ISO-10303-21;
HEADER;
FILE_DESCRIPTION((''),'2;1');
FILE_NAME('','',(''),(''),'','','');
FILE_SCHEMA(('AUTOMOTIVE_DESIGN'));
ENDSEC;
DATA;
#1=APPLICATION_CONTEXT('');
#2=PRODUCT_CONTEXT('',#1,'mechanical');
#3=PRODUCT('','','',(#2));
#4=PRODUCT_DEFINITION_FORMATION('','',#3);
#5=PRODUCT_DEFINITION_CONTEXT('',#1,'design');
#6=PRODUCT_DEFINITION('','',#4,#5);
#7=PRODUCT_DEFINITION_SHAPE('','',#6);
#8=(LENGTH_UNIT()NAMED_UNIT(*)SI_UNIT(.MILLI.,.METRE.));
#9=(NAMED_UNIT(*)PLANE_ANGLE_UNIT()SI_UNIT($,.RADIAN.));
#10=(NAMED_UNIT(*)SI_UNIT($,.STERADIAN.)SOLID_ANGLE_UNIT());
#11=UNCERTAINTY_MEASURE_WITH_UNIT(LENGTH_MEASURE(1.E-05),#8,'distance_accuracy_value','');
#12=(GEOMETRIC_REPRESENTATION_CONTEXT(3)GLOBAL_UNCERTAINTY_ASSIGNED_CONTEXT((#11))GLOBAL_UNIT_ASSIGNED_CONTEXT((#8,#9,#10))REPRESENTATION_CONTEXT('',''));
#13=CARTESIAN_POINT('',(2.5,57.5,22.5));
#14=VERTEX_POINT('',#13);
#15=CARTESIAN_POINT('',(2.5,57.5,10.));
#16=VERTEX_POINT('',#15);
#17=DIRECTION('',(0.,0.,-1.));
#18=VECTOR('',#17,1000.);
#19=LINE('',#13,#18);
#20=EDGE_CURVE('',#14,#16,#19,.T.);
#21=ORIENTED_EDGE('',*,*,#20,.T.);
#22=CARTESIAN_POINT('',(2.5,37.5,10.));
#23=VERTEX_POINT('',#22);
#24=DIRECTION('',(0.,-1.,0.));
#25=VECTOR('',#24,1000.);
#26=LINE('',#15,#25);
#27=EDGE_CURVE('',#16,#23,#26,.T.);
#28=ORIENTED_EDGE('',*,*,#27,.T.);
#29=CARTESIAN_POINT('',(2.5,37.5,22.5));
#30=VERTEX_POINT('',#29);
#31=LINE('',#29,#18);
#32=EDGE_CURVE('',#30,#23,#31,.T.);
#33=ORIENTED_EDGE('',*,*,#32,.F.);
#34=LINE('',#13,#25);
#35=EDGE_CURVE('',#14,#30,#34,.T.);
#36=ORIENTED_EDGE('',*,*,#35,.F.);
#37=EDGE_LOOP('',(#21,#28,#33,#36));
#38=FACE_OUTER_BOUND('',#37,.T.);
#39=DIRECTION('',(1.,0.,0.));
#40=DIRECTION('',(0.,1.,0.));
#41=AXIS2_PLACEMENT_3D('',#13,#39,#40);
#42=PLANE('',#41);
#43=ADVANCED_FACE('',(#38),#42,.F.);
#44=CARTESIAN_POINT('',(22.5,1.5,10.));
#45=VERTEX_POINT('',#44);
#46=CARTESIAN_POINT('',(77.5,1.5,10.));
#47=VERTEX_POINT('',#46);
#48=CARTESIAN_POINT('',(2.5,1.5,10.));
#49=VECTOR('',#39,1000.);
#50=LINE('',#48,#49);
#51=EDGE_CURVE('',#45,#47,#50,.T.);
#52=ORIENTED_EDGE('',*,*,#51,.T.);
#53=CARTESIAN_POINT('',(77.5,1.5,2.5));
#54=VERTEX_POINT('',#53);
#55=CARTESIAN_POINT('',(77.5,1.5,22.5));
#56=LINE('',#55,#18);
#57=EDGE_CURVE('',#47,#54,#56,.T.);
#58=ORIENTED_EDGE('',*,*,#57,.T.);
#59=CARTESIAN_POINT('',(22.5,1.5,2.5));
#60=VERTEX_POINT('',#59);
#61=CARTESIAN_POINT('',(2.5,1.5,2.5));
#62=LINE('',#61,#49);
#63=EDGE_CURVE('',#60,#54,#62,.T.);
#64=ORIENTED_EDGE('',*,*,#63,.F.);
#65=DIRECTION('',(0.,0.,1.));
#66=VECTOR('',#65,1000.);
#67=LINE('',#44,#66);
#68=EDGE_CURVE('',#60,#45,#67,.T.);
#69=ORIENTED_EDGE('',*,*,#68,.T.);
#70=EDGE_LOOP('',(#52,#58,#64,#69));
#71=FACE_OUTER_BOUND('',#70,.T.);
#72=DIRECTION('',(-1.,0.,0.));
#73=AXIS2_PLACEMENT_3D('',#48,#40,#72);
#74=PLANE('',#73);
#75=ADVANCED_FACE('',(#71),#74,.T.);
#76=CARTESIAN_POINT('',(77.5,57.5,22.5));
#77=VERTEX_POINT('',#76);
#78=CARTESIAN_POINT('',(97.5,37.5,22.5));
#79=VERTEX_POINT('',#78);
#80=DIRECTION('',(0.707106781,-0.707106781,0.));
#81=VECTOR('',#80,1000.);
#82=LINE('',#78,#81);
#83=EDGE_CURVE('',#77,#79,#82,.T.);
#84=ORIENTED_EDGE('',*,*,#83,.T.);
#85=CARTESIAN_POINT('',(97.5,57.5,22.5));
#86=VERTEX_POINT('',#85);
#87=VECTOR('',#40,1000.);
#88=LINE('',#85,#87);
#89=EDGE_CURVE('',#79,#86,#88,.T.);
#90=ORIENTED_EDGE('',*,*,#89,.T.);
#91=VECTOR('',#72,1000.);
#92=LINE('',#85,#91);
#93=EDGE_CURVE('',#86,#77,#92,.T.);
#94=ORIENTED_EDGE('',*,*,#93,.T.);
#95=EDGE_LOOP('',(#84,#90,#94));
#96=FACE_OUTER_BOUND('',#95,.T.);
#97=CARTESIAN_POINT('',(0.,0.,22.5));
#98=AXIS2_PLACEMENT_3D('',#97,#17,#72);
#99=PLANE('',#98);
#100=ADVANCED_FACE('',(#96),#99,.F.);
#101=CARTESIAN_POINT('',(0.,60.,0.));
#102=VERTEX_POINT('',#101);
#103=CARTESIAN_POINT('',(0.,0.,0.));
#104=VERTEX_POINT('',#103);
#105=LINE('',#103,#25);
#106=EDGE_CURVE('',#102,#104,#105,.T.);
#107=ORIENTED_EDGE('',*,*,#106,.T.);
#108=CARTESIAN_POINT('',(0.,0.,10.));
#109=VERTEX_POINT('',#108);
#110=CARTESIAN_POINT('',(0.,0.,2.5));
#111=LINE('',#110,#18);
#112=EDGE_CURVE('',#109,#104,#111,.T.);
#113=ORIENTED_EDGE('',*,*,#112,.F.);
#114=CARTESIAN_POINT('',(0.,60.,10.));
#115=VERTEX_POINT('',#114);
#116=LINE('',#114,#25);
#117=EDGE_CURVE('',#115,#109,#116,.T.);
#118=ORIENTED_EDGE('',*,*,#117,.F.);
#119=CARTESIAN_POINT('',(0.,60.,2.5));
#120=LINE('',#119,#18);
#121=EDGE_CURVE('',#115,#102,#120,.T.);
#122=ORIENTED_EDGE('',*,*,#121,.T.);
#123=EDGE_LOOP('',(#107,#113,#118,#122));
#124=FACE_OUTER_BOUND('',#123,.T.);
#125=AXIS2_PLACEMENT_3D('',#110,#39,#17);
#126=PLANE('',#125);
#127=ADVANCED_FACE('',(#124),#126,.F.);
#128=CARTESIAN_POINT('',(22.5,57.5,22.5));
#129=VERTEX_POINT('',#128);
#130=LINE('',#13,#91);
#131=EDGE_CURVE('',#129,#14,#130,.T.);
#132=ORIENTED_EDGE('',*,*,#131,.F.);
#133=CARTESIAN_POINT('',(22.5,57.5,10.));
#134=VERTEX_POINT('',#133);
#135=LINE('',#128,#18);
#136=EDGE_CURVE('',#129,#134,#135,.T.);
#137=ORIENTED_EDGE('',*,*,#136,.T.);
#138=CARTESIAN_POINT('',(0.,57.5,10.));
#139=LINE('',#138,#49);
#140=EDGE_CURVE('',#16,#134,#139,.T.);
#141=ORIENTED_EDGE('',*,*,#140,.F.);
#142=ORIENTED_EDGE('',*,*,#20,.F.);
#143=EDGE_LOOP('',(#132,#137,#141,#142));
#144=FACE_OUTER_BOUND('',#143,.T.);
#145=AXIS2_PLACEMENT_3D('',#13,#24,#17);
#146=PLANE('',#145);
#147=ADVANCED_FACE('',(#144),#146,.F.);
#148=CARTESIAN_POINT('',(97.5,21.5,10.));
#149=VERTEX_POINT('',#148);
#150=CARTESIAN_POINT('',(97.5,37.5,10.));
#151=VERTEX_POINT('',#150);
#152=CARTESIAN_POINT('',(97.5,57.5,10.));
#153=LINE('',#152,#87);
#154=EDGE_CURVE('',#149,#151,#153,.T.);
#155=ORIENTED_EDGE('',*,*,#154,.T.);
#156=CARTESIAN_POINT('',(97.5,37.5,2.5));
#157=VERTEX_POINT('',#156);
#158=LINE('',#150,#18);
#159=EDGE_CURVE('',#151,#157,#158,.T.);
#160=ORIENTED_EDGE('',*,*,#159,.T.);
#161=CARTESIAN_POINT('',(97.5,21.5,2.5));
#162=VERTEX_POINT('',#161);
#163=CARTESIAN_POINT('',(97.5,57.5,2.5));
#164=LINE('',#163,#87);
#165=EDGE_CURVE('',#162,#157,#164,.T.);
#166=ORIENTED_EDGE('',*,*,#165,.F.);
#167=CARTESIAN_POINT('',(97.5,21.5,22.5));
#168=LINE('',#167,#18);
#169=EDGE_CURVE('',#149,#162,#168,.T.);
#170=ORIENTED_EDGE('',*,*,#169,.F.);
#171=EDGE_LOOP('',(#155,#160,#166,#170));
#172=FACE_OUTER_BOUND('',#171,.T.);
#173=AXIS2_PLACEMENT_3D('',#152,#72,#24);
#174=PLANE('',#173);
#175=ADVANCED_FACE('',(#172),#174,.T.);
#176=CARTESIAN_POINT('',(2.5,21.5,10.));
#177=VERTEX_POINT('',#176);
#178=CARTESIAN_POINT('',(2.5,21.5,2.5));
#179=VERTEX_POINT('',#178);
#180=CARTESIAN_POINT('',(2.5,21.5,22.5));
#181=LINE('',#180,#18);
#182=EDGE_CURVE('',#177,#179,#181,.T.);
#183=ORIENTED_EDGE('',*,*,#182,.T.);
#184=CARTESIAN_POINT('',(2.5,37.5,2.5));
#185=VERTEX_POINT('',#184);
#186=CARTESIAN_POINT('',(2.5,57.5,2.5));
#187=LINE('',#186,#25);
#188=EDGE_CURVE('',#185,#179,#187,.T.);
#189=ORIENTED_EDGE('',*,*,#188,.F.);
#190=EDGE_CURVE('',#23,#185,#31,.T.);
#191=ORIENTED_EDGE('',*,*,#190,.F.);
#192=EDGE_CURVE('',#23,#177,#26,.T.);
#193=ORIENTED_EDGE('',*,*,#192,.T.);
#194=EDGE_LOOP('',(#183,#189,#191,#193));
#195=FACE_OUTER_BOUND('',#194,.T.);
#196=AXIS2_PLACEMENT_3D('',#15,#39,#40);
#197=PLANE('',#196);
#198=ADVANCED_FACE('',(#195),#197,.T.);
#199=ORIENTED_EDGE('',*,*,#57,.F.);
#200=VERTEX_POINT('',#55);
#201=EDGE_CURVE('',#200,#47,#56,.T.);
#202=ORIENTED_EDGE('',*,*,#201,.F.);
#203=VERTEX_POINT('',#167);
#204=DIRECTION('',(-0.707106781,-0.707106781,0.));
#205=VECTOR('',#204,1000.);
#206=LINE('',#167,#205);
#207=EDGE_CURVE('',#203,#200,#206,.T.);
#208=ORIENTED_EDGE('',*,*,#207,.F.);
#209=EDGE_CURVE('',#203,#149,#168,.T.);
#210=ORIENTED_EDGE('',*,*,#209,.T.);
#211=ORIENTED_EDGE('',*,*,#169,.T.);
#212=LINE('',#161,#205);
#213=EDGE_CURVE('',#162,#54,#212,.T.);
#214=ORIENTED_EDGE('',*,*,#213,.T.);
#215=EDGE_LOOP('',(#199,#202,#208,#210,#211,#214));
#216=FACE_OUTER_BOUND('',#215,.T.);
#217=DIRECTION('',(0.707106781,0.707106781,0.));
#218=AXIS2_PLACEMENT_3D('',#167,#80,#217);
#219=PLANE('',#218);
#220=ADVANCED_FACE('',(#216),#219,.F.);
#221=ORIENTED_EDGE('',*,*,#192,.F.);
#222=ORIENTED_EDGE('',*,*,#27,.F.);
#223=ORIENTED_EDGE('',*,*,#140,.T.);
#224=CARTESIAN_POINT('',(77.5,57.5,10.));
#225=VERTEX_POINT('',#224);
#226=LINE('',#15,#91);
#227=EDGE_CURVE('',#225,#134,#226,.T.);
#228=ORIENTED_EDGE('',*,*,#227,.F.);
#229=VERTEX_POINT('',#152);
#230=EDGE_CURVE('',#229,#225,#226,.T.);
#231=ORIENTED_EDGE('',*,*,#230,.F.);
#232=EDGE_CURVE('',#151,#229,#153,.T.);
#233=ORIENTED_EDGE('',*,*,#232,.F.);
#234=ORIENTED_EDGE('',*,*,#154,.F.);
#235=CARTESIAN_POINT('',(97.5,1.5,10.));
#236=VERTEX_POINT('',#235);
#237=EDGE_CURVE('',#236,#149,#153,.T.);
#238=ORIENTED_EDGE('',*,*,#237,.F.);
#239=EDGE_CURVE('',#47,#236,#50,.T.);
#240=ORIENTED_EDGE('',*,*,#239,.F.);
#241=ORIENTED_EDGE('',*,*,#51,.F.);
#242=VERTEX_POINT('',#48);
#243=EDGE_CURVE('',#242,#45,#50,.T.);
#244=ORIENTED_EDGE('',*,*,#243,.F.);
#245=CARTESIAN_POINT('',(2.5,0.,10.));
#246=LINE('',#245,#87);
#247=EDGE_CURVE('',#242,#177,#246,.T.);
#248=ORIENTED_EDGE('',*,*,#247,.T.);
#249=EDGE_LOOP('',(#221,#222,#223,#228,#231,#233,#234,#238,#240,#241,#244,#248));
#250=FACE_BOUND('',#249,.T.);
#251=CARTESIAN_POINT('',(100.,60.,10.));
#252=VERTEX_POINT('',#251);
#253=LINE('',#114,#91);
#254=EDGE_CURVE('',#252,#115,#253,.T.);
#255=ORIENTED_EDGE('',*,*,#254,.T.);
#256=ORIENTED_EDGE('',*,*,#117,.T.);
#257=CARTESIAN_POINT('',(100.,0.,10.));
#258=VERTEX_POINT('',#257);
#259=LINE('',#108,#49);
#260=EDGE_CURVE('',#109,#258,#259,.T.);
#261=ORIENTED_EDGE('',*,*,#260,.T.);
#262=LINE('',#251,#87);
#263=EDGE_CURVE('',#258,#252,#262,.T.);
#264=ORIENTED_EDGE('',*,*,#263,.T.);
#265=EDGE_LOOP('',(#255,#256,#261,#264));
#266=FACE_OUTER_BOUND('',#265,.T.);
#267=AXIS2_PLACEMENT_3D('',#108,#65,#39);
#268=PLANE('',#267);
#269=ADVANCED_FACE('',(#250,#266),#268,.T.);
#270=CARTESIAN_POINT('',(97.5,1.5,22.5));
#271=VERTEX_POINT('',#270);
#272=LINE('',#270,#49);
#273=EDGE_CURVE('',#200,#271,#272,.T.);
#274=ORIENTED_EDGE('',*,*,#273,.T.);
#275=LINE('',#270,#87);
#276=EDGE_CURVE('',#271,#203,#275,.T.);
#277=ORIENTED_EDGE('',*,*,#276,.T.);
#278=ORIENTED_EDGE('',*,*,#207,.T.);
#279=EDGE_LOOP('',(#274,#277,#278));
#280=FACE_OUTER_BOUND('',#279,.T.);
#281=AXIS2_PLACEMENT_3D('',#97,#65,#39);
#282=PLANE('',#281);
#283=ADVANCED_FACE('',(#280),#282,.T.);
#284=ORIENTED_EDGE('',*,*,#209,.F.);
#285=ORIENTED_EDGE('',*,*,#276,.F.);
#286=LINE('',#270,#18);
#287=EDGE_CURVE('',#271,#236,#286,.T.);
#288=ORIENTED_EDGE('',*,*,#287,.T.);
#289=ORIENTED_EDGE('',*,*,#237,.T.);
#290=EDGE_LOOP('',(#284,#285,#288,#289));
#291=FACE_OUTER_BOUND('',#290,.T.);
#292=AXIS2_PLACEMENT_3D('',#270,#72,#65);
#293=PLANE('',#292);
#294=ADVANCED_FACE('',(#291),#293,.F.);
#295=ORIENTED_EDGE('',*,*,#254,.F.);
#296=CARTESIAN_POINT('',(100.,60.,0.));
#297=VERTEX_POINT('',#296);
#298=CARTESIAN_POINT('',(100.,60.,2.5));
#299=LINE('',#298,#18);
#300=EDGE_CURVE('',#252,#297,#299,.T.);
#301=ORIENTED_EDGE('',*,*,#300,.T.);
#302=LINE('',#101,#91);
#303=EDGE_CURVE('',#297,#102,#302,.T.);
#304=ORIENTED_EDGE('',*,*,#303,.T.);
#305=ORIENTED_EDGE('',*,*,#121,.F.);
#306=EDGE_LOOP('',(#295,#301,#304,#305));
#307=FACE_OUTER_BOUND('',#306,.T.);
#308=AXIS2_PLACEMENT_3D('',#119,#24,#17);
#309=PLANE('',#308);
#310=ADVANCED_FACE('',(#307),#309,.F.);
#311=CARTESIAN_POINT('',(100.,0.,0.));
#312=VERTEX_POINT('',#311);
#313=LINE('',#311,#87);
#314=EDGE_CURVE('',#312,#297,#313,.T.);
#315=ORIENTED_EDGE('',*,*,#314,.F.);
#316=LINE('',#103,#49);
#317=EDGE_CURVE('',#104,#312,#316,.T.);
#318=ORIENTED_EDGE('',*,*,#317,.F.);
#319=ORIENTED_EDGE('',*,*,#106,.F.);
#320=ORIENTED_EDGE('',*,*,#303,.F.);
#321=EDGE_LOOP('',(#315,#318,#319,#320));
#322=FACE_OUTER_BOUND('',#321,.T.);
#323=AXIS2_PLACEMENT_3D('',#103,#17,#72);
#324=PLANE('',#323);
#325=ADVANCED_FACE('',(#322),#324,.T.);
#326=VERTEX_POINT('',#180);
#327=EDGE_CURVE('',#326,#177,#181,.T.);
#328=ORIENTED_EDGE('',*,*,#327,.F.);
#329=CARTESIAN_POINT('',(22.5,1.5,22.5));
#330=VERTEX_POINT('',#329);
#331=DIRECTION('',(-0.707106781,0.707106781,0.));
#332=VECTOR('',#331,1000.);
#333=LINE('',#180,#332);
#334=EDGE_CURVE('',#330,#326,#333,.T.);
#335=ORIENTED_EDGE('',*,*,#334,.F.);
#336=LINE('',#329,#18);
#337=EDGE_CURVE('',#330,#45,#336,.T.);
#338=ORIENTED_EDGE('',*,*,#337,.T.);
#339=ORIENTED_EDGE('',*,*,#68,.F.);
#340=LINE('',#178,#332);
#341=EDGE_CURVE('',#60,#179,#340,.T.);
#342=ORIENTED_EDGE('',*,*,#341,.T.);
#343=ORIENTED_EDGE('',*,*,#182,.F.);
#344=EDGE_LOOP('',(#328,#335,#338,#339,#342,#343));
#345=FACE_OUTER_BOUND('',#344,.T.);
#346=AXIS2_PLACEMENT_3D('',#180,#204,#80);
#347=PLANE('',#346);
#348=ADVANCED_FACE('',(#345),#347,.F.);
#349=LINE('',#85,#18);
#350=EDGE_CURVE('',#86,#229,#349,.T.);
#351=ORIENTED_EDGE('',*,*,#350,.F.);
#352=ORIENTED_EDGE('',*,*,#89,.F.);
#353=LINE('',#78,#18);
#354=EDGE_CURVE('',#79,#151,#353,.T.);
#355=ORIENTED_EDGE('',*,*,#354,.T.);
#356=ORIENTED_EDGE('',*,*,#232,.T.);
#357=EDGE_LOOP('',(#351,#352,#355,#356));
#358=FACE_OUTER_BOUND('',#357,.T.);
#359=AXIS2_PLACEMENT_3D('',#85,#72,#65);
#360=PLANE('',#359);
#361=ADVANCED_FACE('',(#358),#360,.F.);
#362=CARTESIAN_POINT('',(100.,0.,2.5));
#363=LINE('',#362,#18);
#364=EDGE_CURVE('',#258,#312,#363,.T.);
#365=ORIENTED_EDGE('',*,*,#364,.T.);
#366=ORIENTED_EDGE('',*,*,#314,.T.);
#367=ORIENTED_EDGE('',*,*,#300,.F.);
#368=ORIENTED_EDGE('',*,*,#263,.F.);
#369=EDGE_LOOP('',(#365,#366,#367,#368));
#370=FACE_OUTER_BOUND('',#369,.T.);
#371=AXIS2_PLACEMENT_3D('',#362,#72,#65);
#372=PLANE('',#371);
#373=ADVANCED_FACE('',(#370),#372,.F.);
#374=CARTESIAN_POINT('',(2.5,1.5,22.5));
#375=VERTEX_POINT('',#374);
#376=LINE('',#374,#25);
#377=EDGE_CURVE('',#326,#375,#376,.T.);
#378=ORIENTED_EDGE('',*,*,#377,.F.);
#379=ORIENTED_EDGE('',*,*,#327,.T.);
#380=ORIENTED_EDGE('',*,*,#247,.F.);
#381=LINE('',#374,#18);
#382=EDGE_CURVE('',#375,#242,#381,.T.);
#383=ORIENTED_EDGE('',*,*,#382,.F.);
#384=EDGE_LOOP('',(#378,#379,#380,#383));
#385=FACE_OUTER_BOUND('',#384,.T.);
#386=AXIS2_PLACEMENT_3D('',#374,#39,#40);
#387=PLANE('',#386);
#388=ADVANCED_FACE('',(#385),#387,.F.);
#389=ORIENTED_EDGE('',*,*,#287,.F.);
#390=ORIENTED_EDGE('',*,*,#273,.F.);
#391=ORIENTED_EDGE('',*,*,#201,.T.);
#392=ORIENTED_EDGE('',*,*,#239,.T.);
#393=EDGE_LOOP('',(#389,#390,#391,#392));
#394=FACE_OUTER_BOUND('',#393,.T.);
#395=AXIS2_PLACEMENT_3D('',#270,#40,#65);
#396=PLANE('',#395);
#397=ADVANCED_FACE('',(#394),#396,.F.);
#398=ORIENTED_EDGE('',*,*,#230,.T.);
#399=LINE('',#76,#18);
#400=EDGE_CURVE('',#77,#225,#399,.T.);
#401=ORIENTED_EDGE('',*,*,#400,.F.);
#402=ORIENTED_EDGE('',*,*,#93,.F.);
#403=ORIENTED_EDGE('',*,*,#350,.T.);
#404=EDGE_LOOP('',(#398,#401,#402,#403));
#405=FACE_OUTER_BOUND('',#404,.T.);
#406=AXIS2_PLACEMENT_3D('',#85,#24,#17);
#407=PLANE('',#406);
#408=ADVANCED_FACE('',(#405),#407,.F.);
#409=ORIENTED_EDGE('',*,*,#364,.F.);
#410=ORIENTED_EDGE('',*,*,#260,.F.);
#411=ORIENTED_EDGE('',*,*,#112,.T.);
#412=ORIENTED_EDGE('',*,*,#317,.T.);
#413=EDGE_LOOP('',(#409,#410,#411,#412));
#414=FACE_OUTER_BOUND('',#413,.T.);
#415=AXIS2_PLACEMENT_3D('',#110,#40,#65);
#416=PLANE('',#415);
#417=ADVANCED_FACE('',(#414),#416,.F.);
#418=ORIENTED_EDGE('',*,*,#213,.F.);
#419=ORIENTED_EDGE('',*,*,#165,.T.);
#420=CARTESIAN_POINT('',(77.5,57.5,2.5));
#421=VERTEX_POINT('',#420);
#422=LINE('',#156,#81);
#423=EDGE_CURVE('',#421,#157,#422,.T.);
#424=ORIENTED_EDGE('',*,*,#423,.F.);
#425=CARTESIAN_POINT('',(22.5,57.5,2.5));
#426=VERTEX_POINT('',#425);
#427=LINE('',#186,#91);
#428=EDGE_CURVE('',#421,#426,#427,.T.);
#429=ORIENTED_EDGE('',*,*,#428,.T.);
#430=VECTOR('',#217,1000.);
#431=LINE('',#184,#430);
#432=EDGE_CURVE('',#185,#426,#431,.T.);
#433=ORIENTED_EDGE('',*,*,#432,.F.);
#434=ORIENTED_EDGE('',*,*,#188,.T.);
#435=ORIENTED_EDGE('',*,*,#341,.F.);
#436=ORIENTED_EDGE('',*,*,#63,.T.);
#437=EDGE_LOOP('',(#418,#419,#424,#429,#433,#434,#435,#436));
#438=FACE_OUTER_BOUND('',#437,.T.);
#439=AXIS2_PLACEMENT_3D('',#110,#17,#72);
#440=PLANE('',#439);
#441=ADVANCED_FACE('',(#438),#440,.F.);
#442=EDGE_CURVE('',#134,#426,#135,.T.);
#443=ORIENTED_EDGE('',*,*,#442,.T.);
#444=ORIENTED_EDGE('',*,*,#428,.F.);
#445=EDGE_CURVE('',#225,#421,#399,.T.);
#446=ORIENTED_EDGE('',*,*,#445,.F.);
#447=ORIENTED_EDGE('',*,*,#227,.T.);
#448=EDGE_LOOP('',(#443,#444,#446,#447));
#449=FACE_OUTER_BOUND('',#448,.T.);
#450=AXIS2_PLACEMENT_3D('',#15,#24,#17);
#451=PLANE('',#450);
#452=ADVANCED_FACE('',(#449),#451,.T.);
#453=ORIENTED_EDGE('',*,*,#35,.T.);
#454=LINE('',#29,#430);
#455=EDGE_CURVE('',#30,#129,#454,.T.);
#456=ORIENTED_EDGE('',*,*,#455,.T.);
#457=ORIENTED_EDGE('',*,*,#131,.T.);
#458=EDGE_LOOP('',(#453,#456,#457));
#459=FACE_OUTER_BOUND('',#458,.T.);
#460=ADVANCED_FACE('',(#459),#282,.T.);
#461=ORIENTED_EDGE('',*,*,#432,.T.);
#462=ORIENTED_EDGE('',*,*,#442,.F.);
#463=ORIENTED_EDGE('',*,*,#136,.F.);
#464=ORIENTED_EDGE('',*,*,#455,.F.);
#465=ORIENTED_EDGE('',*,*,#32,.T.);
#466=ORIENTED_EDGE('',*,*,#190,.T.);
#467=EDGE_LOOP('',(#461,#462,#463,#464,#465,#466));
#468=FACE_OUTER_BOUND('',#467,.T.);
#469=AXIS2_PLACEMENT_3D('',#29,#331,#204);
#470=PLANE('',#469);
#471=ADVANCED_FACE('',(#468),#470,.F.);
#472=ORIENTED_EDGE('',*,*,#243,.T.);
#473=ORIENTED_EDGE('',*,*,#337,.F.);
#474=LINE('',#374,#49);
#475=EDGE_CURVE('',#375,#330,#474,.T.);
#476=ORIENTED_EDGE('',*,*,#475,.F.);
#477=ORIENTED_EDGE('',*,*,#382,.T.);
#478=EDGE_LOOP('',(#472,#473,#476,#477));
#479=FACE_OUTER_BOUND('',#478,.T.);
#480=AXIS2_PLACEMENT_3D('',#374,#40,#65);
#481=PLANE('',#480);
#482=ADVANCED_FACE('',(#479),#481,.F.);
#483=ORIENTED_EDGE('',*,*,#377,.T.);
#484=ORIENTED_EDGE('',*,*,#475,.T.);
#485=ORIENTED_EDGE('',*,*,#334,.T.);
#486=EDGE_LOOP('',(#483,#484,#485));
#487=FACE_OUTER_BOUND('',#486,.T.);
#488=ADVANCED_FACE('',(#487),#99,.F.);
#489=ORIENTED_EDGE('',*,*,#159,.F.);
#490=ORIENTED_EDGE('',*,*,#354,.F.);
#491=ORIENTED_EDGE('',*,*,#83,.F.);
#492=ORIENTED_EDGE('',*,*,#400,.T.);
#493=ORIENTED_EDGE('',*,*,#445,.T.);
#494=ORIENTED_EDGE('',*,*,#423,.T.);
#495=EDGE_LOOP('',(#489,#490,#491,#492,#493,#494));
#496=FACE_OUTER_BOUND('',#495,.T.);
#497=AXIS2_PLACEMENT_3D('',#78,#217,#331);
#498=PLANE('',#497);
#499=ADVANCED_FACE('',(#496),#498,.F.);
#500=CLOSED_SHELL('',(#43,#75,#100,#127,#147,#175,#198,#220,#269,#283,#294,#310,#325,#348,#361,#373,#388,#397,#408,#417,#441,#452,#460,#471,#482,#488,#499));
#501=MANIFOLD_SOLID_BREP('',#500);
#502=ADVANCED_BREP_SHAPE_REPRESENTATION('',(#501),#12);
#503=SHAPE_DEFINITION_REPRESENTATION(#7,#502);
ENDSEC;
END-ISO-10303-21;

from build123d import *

# Parameters (mm, degrees)
BASE_PLATE_PROFILE_W      = 100
BASE_PLATE_PROFILE_H      = 60
BASE_PLATE_2_5MM_DEPTH    = 2.5
RIM_WALL_PROFILE_W        = 100
RIM_WALL_PROFILE_H        = 60
RIM_WALL_PROFILE_W_2      = 95
RIM_WALL_PROFILE_H_2      = 56
RIM_WALL_7_5MM_DEPTH      = 7.5
CORNER_GUSSETS_20MM_DEPTH = 20


with BuildPart() as part:
    # Base Plate Profile → Base Plate 2.5mm (new body)
    with BuildSketch(Plane.XY):
        with Locations((50, 30)):
            Rectangle(BASE_PLATE_PROFILE_W, BASE_PLATE_PROFILE_H)
    extrude(amount=BASE_PLATE_2_5MM_DEPTH)

    # Rim Wall Profile → Rim Wall 7.5mm (add)
    with BuildSketch(Plane.XY.offset(2.5)):
        with Locations((50, 30)):
            Rectangle(RIM_WALL_PROFILE_W, RIM_WALL_PROFILE_H)
        with Locations((50, 29.5)):
            Rectangle(RIM_WALL_PROFILE_W_2, RIM_WALL_PROFILE_H_2, mode=Mode.SUBTRACT)
    extrude(amount=RIM_WALL_7_5MM_DEPTH)

    # Corner Gusset Profile → Corner Gussets 20mm (add)
    with BuildSketch(Plane.XY.offset(2.5)):
        Polygon((2.5, 57.5), (22.5, 57.5), (2.5, 37.5), align=None)
        Polygon((2.5, 1.5), (22.5, 1.5), (2.5, 21.5), align=None)
        Polygon((97.5, 57.5), (77.5, 57.5), (97.5, 37.5), align=None)
        Polygon((97.5, 1.5), (77.5, 1.5), (97.5, 21.5), align=None)
    extrude(amount=CORNER_GUSSETS_20MM_DEPTH)


solid = part.part
